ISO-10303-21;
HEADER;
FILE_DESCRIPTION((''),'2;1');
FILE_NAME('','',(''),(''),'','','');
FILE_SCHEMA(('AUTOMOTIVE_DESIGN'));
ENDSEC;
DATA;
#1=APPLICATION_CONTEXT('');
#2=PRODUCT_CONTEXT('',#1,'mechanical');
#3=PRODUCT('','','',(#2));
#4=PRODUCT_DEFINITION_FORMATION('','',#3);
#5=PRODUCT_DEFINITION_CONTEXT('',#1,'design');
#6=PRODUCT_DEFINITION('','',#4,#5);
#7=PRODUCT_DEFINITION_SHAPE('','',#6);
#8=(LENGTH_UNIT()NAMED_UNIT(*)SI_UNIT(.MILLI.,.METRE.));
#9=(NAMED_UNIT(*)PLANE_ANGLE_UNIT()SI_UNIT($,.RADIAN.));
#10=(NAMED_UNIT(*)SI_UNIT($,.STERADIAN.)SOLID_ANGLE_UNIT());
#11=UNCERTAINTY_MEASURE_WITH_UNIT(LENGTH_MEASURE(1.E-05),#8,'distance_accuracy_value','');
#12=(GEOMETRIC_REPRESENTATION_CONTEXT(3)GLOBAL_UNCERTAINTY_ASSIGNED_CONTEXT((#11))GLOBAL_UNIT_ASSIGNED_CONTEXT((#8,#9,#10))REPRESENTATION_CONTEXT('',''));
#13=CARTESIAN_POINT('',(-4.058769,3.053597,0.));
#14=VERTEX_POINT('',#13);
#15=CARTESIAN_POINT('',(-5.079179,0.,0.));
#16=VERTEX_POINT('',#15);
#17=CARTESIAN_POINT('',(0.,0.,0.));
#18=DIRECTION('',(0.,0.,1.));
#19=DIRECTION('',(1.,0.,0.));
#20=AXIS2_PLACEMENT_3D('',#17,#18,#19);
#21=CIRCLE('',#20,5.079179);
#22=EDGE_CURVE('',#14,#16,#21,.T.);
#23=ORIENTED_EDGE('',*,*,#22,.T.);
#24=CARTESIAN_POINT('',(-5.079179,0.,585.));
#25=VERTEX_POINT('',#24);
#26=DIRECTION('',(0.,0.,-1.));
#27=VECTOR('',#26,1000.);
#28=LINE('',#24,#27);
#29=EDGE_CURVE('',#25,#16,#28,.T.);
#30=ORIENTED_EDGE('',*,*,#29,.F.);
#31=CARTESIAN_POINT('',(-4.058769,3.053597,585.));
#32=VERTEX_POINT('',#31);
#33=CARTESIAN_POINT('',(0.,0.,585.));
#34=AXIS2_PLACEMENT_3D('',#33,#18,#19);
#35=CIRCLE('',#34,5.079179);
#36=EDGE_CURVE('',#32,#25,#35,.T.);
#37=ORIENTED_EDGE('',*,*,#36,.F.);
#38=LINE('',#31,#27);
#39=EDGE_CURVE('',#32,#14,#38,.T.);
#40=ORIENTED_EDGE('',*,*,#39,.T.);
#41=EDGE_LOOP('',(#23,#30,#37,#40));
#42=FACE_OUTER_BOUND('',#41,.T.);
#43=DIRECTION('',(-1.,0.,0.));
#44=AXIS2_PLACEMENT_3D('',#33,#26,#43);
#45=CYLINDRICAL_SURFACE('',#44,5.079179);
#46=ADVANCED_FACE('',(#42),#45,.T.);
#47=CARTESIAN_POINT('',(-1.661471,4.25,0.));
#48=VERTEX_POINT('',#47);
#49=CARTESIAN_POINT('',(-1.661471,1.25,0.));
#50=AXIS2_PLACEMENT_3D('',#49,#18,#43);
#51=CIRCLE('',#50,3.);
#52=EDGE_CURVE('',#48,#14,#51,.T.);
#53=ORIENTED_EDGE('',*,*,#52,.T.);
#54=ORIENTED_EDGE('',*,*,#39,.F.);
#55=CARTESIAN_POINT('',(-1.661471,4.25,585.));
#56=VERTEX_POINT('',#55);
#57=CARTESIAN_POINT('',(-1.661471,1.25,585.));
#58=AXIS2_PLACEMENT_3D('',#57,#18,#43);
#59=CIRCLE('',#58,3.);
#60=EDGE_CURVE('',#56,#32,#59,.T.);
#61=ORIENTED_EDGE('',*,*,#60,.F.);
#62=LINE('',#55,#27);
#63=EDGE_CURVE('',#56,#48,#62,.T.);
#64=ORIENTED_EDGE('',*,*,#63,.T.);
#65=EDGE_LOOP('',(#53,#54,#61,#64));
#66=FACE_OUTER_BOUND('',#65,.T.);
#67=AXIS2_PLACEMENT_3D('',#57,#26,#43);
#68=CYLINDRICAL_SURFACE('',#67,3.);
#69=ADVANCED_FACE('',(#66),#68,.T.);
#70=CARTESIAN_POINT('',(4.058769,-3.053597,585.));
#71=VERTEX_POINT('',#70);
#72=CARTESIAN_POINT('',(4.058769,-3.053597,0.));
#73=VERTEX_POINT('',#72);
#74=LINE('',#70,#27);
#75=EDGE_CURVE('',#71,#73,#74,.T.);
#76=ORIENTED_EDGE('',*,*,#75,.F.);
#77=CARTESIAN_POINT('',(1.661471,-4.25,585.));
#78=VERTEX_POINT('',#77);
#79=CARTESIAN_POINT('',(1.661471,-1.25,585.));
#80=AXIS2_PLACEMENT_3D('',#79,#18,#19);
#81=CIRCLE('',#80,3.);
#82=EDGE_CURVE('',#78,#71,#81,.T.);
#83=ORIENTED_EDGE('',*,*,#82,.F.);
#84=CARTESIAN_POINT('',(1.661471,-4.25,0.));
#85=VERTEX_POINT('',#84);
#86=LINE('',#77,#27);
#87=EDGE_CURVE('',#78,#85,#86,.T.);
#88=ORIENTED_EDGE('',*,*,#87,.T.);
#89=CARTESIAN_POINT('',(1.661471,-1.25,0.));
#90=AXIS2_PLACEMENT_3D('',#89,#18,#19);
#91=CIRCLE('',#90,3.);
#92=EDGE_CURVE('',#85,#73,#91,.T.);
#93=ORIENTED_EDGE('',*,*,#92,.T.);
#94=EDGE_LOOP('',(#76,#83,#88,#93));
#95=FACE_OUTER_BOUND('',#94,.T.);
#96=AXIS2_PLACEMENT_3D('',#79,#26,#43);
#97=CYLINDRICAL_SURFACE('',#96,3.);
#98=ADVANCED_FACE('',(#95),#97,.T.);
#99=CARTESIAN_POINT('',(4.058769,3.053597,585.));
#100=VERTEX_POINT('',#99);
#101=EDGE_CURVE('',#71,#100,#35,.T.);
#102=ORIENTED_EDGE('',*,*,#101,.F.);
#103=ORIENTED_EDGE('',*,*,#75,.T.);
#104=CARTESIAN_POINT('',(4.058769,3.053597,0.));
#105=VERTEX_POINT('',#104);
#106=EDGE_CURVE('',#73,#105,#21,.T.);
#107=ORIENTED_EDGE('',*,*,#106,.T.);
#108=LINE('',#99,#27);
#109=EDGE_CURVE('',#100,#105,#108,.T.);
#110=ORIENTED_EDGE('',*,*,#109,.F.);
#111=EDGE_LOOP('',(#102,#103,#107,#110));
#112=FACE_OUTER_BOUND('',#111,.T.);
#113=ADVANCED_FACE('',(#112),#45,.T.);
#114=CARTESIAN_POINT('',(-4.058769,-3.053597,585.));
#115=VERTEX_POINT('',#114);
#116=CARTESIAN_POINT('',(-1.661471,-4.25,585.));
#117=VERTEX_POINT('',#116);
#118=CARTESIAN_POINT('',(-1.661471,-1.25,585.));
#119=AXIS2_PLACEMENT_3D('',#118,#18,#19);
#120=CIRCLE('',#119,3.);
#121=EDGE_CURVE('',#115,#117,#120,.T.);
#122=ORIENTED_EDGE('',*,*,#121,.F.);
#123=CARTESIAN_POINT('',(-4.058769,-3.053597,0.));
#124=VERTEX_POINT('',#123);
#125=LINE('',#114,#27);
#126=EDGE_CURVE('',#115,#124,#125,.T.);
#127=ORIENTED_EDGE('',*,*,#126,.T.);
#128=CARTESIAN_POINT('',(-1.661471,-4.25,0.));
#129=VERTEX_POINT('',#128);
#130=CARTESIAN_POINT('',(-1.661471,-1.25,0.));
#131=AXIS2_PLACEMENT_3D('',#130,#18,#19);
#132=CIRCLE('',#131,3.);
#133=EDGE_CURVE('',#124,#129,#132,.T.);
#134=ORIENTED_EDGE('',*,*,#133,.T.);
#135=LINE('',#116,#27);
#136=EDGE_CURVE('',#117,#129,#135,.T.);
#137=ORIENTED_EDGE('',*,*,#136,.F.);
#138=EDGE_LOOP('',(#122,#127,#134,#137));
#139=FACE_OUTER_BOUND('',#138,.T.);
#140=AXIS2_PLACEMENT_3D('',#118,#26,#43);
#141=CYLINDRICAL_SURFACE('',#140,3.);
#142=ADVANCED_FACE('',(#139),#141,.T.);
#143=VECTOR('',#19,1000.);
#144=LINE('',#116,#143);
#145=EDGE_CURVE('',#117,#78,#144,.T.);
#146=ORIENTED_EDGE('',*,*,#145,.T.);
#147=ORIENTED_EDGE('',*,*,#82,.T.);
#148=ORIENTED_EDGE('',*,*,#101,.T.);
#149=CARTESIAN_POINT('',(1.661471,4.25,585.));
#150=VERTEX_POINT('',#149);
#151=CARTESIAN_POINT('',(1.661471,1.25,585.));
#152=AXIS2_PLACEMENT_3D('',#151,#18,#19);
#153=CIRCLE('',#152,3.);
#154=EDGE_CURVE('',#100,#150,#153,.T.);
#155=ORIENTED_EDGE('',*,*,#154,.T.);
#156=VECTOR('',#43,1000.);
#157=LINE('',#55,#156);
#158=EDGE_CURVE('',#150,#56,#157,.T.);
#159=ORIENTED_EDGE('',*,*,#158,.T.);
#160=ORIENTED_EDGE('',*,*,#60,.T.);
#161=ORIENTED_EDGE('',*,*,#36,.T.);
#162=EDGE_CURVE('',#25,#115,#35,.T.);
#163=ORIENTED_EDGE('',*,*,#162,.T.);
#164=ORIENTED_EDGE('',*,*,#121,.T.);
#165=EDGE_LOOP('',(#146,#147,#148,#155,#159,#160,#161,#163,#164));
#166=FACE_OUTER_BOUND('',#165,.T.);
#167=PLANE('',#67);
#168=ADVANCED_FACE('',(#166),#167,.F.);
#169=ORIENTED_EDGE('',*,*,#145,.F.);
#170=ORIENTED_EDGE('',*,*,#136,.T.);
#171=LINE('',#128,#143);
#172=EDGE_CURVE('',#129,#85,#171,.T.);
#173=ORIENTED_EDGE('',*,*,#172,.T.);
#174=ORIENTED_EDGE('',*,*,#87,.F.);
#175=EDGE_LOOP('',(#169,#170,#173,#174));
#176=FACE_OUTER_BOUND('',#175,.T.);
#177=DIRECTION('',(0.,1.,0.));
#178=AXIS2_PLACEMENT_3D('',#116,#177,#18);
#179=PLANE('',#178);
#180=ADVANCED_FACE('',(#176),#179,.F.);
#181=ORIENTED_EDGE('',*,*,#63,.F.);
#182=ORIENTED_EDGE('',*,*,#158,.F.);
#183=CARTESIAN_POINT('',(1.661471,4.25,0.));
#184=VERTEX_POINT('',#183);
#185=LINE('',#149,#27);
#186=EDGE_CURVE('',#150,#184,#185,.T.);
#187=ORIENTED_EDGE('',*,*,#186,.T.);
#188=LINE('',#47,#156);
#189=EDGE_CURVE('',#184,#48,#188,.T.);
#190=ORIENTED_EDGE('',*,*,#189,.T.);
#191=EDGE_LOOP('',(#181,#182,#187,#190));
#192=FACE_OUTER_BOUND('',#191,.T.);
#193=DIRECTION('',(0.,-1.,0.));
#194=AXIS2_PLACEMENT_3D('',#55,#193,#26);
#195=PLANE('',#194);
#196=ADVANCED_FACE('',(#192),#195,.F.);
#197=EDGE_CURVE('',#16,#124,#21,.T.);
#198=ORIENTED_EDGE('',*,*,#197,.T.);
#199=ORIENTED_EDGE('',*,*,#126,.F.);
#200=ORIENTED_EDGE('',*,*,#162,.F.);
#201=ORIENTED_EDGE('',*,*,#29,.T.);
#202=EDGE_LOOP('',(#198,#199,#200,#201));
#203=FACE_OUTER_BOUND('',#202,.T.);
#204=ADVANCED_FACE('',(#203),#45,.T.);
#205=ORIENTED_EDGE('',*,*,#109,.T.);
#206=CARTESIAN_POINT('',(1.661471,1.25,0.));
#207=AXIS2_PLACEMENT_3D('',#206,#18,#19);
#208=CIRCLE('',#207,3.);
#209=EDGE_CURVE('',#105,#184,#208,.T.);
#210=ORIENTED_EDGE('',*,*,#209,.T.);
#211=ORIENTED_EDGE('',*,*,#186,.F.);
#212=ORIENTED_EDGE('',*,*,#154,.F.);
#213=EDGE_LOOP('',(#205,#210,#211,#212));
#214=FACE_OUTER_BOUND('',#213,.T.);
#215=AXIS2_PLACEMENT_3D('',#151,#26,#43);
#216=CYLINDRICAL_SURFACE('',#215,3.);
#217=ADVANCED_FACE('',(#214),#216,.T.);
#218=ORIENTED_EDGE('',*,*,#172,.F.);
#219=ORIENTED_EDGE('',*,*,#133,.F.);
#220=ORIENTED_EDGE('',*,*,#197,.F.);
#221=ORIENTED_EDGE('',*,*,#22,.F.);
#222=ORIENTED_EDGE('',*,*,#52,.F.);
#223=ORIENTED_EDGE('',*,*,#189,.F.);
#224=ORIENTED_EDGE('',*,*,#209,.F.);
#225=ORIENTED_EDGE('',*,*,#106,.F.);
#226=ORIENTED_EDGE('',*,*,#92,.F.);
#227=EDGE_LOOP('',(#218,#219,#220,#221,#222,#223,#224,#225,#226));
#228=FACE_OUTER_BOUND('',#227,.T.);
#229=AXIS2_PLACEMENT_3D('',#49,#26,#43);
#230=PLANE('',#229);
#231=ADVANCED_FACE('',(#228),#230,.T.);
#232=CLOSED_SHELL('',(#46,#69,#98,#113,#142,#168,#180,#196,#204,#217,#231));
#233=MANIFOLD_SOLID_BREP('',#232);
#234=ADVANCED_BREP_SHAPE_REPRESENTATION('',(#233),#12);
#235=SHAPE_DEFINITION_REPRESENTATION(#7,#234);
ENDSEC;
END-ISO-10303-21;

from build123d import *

# Parameters (mm, degrees)
EXTRUDE_1_DEPTH = 585


with BuildPart() as part:
    # 草图1 → 拉伸1 (new body)
    with BuildSketch(Plane.XY):
        with BuildLine():
            Line((-1.661470687, 4.25), (1.661470687, 4.25))
            ThreePointArc((1.661470687, 4.25), (3.001099397, 3.934286669), (4.058769011, 3.053596614))
            ThreePointArc((4.058769011, 3.053596614), (5.079178887, 0), (4.058769011, -3.053596614))
            ThreePointArc((4.058769011, -3.053596614), (3.001099397, -3.934286669), (1.661470687, -4.25))
            Line((1.661470687, -4.25), (-1.661470687, -4.25))
            ThreePointArc((-1.661470687, -4.25), (-3.001099397, -3.934286669), (-4.058769011, -3.053596614))
            ThreePointArc((-4.058769011, -3.053596614), (-5.079178887, 0), (-4.058769011, 3.053596614))
            ThreePointArc((-4.058769011, 3.053596614), (-3.001099397, 3.934286669), (-1.661470687, 4.25))
        make_face()
    extrude(amount=EXTRUDE_1_DEPTH)


solid = part.part
